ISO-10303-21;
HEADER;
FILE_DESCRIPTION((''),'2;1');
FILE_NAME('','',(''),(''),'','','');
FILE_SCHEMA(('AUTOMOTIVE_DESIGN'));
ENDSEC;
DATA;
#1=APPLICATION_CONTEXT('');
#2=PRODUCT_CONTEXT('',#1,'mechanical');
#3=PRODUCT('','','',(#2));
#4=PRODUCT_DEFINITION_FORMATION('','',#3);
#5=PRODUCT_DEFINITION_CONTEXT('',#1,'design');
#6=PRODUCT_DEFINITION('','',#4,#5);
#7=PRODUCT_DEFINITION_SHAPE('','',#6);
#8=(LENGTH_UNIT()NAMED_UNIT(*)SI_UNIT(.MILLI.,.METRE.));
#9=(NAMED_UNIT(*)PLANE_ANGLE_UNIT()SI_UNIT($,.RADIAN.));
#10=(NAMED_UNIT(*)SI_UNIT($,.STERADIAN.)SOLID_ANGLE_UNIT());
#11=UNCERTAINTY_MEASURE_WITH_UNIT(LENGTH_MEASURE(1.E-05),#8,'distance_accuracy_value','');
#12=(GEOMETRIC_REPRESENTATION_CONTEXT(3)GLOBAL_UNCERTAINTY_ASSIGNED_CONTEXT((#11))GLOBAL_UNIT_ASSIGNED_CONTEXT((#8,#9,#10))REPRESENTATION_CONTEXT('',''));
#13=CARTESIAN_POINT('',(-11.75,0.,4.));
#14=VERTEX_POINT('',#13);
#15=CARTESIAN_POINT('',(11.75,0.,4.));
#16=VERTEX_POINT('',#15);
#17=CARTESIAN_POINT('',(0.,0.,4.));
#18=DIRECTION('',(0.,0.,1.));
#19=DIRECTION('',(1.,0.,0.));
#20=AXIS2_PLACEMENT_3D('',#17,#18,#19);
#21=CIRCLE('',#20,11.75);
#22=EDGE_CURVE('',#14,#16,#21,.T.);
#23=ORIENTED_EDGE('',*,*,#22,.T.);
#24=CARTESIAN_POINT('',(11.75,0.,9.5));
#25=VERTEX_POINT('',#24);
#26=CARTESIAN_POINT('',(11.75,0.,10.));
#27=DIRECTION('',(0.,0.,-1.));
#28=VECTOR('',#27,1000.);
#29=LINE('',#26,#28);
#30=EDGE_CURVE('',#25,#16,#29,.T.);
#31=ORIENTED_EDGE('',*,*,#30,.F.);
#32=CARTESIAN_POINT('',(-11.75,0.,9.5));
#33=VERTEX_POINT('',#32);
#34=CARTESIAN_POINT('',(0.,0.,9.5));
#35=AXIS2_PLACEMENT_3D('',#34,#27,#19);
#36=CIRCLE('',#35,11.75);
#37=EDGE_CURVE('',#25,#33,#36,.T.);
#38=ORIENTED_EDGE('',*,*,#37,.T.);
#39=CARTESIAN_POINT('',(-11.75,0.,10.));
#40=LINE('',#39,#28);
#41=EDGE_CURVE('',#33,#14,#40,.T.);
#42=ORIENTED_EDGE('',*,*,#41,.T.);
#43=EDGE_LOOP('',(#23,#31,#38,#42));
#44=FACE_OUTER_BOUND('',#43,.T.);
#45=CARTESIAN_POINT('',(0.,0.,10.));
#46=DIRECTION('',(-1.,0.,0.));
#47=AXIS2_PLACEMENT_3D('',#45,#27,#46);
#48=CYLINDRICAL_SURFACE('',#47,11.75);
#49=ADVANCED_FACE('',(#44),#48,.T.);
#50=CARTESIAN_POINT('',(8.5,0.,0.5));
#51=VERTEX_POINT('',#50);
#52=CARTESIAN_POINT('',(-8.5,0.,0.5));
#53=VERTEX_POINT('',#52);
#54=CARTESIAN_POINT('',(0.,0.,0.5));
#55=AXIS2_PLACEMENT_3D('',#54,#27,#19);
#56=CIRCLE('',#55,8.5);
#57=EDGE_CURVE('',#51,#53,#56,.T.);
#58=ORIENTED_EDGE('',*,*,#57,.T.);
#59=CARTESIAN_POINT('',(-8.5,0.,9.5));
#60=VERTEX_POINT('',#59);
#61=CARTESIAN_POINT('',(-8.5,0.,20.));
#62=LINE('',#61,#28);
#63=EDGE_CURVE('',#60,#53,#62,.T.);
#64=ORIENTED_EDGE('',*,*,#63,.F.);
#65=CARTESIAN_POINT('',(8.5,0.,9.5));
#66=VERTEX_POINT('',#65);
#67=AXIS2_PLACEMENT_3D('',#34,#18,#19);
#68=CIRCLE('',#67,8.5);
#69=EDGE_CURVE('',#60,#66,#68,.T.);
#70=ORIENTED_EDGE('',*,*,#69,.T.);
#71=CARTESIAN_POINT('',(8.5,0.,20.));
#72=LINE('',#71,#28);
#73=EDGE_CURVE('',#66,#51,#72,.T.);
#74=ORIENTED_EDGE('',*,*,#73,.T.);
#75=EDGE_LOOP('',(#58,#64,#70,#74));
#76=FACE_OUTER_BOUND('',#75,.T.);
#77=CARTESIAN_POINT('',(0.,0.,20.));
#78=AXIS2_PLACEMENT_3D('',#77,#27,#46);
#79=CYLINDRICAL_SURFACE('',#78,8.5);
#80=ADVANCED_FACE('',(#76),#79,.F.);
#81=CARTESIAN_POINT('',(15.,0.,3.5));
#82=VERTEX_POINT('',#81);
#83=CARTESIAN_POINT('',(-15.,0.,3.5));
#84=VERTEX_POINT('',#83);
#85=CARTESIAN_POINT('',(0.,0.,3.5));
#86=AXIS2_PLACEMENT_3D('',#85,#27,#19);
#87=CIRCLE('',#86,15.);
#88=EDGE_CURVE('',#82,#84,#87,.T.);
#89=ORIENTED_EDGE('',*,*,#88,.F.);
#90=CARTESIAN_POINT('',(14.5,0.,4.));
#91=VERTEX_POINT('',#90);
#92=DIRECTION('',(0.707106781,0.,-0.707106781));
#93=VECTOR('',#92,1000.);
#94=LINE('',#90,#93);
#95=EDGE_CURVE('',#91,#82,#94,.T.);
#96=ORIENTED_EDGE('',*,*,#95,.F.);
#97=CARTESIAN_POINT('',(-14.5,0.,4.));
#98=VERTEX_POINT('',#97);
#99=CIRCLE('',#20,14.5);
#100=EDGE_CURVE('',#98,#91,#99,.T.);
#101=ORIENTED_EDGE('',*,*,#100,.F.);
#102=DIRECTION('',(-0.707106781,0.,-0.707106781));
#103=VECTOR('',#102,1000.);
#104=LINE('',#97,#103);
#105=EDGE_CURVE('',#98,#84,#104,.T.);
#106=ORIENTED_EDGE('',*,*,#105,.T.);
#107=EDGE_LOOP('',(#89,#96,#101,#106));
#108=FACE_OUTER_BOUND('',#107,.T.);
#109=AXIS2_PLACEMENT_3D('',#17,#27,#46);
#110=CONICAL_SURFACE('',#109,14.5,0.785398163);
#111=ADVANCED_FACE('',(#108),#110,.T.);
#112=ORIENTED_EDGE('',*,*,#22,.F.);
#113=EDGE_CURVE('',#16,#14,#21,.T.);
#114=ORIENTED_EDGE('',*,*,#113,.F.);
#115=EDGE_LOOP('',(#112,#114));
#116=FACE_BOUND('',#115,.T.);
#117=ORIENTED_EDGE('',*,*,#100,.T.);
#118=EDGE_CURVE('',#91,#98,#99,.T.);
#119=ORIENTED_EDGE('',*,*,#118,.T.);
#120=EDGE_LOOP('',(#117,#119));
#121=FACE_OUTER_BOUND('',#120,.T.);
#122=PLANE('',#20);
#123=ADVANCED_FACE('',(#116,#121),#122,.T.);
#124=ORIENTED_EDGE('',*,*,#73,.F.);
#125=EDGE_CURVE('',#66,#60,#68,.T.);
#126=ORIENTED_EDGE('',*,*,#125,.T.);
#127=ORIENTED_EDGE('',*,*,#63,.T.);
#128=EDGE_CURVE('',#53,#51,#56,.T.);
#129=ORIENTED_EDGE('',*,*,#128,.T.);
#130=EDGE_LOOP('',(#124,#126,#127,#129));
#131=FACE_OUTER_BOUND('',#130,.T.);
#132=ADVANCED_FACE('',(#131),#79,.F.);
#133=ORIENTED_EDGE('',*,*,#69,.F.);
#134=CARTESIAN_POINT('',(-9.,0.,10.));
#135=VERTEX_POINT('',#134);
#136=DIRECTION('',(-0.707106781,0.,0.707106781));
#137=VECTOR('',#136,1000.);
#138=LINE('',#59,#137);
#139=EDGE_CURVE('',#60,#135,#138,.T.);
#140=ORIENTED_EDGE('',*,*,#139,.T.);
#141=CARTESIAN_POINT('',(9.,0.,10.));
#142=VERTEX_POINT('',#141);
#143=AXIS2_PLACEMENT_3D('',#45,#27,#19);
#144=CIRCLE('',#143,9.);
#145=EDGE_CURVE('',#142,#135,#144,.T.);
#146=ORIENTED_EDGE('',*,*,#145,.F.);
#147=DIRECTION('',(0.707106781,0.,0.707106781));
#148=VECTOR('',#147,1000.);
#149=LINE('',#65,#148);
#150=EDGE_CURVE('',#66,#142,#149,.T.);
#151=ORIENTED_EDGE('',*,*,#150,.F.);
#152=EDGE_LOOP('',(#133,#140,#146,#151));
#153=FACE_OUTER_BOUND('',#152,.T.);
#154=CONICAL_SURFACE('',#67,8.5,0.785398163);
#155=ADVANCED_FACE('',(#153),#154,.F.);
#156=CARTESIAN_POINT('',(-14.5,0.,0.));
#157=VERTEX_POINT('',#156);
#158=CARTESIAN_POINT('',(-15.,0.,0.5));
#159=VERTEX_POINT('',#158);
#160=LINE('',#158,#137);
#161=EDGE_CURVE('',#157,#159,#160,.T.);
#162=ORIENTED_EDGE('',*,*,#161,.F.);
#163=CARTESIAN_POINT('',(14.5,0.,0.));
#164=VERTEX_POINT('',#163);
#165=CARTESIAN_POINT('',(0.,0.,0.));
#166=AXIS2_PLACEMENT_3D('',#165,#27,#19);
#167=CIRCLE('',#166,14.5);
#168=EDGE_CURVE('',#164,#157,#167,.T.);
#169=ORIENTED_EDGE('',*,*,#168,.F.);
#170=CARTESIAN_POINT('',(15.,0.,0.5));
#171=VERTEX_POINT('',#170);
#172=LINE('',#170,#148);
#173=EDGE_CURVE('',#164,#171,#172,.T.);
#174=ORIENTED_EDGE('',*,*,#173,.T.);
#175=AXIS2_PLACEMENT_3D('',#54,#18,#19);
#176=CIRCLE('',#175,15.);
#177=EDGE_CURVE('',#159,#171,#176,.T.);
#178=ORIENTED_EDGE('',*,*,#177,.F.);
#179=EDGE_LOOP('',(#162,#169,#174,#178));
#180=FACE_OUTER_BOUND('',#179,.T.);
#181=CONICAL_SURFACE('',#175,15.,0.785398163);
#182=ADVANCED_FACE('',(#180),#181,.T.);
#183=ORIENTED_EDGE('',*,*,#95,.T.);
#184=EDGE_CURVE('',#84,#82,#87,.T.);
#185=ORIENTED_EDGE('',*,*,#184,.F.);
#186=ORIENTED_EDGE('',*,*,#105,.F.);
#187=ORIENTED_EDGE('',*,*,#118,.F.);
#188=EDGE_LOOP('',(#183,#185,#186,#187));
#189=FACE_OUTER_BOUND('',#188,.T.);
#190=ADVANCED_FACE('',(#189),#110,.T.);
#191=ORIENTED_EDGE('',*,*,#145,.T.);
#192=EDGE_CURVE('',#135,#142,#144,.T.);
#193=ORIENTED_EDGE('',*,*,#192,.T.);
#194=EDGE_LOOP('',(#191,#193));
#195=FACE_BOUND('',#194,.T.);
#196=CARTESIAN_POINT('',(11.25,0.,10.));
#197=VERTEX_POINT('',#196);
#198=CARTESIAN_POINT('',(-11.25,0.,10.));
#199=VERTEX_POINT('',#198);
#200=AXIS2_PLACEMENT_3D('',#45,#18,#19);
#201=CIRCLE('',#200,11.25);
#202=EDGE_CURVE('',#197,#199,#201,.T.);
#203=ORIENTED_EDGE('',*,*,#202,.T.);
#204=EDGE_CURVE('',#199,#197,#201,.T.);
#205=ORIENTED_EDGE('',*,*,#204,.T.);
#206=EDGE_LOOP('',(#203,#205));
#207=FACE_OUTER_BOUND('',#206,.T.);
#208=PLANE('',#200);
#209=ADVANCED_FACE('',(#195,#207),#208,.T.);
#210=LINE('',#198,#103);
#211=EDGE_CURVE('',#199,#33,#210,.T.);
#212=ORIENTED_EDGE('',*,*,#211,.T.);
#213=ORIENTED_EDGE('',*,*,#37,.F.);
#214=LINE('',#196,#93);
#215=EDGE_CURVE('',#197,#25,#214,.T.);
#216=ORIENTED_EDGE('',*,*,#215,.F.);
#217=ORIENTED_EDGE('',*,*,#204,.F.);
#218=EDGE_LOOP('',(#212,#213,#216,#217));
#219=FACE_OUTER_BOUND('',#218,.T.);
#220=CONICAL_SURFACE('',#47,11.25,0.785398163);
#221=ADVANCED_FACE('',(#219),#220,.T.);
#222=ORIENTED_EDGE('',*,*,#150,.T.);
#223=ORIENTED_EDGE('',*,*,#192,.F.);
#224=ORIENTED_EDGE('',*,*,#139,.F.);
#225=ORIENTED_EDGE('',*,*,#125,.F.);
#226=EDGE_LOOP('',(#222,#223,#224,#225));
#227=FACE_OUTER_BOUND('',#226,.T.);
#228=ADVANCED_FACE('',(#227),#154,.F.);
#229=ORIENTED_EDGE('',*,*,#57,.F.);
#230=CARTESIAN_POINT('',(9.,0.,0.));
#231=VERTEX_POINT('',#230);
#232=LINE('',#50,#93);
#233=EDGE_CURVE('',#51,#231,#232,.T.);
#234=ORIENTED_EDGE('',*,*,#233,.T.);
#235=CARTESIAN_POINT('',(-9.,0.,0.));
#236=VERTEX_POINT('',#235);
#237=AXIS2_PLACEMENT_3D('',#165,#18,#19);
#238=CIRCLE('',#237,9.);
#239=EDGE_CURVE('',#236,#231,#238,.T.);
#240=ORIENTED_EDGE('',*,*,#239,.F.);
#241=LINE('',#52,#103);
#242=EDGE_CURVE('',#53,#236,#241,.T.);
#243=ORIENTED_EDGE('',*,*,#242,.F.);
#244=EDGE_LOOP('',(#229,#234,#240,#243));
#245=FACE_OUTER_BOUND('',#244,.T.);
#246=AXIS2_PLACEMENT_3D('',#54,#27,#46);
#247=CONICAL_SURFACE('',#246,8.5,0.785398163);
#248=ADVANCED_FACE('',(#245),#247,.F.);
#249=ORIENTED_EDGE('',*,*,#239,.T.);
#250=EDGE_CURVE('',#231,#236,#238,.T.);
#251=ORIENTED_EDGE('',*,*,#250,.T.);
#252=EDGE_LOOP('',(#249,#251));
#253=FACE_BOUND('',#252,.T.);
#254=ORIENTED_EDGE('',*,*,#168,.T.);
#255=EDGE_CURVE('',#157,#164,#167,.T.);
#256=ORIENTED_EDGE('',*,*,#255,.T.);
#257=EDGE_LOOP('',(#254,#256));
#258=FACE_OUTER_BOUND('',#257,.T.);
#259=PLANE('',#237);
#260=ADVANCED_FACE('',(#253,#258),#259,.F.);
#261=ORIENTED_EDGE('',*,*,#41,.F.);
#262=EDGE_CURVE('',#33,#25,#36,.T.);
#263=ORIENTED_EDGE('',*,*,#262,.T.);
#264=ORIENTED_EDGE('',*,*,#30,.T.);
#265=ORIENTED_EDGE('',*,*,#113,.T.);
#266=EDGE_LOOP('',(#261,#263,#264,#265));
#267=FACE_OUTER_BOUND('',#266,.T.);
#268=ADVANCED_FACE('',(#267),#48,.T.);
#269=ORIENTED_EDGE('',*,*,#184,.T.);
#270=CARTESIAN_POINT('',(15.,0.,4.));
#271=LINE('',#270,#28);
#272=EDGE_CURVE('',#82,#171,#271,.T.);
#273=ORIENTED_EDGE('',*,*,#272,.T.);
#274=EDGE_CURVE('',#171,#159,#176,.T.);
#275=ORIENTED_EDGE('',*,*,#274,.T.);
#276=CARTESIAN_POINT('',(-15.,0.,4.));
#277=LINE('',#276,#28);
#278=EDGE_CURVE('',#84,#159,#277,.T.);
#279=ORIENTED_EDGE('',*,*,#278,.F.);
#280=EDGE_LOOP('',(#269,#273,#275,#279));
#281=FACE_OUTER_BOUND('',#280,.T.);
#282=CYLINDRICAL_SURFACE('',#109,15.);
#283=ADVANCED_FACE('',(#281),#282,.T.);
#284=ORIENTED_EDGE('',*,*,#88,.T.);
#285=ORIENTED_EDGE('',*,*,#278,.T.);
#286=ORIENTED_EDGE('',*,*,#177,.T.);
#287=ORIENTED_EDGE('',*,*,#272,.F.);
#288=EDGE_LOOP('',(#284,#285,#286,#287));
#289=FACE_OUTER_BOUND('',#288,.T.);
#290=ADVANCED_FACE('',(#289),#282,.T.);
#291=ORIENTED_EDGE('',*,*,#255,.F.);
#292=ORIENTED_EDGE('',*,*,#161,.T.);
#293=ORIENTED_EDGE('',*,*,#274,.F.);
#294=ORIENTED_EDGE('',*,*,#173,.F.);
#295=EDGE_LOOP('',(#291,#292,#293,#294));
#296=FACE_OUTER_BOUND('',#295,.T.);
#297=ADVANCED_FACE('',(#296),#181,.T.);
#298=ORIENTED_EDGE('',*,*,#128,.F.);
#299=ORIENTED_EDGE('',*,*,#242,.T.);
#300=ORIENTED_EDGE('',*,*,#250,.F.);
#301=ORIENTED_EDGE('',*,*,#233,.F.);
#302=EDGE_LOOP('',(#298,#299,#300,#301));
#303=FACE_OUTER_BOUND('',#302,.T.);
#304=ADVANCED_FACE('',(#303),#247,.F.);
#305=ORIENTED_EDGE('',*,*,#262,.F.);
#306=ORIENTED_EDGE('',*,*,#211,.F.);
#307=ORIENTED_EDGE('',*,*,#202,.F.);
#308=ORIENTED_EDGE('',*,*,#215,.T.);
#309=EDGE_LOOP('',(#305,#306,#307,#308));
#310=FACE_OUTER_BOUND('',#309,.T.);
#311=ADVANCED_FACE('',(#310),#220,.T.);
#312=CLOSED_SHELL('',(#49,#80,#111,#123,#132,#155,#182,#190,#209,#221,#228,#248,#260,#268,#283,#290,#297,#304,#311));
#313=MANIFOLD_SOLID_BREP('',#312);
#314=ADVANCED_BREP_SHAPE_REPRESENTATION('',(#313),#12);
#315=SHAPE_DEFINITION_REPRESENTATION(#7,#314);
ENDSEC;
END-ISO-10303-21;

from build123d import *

# Parameters (mm, degrees)
SKETCH1_R           = 15
BOSS_EXTRUDE1_DEPTH = 4
SKETCH2_R           = 11.75
BOSS_EXTRUDE2_DEPTH = 6
SKETCH3_R           = 8.5
CUT_EXTRUDE1_DEPTH  = 20
CHAMFER1_SIZE       = 0.5
CHAMFER2_SIZE       = 0.5


with BuildPart() as part:
    # Sketch1 → Boss-Extrude1 (new body)
    with BuildSketch(Plane.XY):
        Circle(SKETCH1_R)
    extrude(amount=BOSS_EXTRUDE1_DEPTH)

    # Sketch2 → Boss-Extrude2 (add)
    with BuildSketch(Plane.XY.offset(4)):
        Circle(SKETCH2_R)
    extrude(amount=BOSS_EXTRUDE2_DEPTH)

    # Sketch3 → Cut-Extrude1 (cut)
    with BuildSketch(Plane(origin=(0, 0, 0), x_dir=(-1, 0, 0), z_dir=(0, 0, -1))):
        Circle(SKETCH3_R)
    extrude(amount=-CUT_EXTRUDE1_DEPTH, mode=Mode.SUBTRACT)

    # Chamfer1
    chamfer1_edges = [part.edges().sort_by_distance(p)[0] for p in [
        (8.5, 0, 10),
        (8.5, 0, 0),
    ]]
    chamfer(chamfer1_edges, length=CHAMFER1_SIZE)

    # Chamfer2
    chamfer2_edges = [part.edges().sort_by_distance(p)[0] for p in [
        (-15, 0, 0),
        (-15, 0, 4),
        (-11.75, 0, 10),
    ]]
    chamfer(chamfer2_edges, length=CHAMFER2_SIZE)


solid = part.part
